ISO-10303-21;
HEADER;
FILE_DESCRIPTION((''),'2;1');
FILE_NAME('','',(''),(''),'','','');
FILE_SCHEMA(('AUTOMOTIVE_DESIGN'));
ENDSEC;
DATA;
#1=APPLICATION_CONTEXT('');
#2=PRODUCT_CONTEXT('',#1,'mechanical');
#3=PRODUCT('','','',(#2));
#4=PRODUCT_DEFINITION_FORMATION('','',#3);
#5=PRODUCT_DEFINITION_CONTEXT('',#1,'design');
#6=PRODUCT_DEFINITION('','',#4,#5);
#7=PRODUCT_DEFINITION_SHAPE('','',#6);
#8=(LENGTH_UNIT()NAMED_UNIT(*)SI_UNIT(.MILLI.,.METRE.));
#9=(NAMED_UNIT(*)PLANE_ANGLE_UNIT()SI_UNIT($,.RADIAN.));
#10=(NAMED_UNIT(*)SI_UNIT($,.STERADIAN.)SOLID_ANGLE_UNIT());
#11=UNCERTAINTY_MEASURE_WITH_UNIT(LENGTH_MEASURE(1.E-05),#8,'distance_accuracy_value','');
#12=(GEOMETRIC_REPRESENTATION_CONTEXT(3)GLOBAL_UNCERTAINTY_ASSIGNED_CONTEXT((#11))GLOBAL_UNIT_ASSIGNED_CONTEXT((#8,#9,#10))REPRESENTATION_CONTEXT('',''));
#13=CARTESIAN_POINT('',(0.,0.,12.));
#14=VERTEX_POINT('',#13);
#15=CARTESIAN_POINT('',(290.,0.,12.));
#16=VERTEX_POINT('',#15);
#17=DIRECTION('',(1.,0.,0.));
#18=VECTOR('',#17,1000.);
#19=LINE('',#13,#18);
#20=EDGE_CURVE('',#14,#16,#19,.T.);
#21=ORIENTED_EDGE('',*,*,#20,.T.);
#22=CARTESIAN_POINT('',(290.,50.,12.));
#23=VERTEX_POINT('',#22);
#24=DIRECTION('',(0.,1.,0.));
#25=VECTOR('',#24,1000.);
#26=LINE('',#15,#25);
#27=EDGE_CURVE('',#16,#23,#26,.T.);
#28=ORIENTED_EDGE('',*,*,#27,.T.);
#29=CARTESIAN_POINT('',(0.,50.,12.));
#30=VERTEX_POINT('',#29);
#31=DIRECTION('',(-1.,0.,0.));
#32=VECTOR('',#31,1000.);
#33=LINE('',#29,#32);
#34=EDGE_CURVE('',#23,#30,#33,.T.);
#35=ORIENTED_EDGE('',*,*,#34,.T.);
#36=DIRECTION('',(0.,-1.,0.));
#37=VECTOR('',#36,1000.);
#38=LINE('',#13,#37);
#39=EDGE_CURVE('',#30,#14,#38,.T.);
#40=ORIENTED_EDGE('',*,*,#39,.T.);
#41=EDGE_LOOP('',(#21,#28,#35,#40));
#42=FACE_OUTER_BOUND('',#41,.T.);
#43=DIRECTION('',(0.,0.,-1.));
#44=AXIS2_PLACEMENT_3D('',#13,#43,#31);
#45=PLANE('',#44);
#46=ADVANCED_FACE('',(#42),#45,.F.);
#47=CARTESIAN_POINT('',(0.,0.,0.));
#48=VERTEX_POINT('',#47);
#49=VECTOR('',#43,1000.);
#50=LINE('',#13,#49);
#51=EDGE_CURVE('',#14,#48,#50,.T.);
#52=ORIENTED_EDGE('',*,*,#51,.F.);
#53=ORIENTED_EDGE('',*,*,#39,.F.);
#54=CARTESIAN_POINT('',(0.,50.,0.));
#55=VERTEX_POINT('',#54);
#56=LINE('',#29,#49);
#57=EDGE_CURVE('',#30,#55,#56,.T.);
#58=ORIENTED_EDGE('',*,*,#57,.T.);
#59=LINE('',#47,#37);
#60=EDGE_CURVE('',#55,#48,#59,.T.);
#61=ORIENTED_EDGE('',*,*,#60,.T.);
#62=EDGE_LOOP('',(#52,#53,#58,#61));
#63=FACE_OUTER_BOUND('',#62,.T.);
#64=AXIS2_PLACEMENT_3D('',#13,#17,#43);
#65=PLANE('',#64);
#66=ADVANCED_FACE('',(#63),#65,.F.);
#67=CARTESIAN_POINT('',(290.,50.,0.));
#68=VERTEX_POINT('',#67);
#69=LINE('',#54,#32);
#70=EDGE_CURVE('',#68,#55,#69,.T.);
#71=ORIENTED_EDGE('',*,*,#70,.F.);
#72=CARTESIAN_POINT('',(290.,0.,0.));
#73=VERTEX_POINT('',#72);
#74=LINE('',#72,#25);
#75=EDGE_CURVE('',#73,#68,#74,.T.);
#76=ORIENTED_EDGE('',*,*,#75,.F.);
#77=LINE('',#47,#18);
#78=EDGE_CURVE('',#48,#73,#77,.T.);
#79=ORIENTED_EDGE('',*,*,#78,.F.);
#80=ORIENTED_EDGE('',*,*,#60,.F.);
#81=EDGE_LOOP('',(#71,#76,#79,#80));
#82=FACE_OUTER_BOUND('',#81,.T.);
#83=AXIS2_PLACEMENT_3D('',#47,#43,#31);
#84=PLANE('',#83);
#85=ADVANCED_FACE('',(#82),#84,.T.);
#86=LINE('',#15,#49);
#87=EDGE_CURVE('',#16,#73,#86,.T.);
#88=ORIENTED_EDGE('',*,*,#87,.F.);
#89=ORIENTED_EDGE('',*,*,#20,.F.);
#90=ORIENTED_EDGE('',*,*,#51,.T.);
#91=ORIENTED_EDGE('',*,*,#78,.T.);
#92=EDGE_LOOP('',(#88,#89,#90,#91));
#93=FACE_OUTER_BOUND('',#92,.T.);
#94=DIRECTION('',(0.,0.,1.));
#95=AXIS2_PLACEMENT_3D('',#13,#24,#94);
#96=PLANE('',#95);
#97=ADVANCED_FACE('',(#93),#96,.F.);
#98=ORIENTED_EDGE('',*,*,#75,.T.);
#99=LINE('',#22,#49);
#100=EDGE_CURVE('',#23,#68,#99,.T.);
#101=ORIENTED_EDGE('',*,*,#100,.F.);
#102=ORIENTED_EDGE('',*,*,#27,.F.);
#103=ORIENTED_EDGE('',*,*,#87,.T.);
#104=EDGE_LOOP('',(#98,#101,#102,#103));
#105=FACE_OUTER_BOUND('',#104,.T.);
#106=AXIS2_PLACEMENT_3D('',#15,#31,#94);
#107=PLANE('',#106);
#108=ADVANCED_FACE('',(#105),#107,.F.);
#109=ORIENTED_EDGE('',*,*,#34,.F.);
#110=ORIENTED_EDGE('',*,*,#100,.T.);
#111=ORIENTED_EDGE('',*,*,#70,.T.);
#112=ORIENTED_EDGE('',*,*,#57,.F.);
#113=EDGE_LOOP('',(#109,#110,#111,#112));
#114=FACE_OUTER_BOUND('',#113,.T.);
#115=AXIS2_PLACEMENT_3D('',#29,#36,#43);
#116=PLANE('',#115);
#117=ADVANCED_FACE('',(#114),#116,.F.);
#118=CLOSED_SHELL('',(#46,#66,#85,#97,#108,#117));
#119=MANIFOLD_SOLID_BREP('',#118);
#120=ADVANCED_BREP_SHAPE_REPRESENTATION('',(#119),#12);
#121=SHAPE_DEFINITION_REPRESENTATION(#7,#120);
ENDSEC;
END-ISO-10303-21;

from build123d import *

# Parameters (mm, degrees)
SKETCH1_W           = 290
SKETCH1_H           = 50
BOSS_EXTRUDE1_DEPTH = 12


with BuildPart() as part:
    # Sketch1 → Boss-Extrude1 (new body)
    with BuildSketch(Plane.XY):
        with Locations((145, 25)):
            Rectangle(SKETCH1_W, SKETCH1_H)
    extrude(amount=BOSS_EXTRUDE1_DEPTH)


solid = part.part
